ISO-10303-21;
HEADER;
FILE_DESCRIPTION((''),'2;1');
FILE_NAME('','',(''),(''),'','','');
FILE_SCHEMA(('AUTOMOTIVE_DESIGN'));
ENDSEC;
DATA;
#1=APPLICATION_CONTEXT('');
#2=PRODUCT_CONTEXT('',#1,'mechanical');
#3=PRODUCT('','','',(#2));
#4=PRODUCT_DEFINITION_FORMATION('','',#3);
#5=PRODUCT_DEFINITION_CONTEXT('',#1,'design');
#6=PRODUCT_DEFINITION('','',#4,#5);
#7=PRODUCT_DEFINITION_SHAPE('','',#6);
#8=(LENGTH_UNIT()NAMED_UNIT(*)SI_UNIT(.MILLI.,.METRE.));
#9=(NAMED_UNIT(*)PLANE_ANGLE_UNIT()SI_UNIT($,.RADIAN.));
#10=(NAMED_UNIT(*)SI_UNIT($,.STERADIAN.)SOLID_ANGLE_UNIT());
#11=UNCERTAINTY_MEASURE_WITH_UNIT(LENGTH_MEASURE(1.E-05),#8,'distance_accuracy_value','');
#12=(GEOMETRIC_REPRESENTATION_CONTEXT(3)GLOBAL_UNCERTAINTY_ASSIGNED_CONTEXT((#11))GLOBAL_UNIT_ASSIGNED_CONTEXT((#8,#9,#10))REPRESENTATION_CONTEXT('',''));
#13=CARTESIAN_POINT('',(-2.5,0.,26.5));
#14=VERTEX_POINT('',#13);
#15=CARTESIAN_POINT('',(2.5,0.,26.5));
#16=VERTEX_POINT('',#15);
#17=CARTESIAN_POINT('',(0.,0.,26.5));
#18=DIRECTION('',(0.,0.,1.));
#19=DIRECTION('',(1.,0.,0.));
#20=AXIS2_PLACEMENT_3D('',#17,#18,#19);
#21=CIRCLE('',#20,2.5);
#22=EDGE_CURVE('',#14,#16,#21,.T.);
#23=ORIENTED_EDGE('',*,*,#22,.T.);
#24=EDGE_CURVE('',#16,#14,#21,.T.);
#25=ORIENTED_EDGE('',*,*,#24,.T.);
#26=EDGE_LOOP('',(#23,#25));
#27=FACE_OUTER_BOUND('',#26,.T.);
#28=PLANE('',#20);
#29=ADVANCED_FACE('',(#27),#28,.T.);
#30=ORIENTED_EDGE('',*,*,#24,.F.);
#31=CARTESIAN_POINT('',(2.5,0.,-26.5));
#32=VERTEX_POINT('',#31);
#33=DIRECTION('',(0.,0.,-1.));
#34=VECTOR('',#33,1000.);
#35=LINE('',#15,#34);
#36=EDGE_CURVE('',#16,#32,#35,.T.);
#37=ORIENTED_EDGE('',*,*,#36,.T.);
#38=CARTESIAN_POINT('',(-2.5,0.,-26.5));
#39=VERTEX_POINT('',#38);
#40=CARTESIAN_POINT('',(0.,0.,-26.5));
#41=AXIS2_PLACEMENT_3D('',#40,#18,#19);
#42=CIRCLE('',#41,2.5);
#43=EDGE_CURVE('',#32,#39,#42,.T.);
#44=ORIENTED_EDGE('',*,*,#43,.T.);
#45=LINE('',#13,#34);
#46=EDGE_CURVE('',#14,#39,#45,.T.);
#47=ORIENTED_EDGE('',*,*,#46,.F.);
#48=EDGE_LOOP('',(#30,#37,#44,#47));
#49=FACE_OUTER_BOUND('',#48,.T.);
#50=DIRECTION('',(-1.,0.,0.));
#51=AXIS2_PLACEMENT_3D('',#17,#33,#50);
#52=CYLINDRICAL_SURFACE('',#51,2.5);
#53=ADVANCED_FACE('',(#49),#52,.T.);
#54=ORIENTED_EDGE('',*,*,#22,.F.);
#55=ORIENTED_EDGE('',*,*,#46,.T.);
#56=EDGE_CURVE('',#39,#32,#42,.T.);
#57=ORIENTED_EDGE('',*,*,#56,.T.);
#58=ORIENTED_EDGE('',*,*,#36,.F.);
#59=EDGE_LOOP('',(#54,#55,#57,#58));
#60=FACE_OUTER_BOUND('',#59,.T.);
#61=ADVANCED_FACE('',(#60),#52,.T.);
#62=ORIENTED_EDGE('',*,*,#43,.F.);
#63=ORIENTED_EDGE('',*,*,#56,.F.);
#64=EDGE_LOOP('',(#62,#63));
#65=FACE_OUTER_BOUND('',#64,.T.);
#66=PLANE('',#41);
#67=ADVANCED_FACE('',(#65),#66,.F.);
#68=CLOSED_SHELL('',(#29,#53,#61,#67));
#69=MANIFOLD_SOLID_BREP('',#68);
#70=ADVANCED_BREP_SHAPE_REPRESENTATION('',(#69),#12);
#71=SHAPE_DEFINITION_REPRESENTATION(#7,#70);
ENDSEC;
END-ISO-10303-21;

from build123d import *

# Parameters (mm, degrees)
ROD_PROFILE_5_R    = 2.5
ROD_BODY_L53_DEPTH = 26.5


with BuildPart() as part:
    # Rod Profile Ø5 → Rod Body L53 (new, symmetric)
    with BuildSketch(Plane.XY):
        Circle(ROD_PROFILE_5_R)
    extrude(amount=ROD_BODY_L53_DEPTH, both=True)


solid = part.part
